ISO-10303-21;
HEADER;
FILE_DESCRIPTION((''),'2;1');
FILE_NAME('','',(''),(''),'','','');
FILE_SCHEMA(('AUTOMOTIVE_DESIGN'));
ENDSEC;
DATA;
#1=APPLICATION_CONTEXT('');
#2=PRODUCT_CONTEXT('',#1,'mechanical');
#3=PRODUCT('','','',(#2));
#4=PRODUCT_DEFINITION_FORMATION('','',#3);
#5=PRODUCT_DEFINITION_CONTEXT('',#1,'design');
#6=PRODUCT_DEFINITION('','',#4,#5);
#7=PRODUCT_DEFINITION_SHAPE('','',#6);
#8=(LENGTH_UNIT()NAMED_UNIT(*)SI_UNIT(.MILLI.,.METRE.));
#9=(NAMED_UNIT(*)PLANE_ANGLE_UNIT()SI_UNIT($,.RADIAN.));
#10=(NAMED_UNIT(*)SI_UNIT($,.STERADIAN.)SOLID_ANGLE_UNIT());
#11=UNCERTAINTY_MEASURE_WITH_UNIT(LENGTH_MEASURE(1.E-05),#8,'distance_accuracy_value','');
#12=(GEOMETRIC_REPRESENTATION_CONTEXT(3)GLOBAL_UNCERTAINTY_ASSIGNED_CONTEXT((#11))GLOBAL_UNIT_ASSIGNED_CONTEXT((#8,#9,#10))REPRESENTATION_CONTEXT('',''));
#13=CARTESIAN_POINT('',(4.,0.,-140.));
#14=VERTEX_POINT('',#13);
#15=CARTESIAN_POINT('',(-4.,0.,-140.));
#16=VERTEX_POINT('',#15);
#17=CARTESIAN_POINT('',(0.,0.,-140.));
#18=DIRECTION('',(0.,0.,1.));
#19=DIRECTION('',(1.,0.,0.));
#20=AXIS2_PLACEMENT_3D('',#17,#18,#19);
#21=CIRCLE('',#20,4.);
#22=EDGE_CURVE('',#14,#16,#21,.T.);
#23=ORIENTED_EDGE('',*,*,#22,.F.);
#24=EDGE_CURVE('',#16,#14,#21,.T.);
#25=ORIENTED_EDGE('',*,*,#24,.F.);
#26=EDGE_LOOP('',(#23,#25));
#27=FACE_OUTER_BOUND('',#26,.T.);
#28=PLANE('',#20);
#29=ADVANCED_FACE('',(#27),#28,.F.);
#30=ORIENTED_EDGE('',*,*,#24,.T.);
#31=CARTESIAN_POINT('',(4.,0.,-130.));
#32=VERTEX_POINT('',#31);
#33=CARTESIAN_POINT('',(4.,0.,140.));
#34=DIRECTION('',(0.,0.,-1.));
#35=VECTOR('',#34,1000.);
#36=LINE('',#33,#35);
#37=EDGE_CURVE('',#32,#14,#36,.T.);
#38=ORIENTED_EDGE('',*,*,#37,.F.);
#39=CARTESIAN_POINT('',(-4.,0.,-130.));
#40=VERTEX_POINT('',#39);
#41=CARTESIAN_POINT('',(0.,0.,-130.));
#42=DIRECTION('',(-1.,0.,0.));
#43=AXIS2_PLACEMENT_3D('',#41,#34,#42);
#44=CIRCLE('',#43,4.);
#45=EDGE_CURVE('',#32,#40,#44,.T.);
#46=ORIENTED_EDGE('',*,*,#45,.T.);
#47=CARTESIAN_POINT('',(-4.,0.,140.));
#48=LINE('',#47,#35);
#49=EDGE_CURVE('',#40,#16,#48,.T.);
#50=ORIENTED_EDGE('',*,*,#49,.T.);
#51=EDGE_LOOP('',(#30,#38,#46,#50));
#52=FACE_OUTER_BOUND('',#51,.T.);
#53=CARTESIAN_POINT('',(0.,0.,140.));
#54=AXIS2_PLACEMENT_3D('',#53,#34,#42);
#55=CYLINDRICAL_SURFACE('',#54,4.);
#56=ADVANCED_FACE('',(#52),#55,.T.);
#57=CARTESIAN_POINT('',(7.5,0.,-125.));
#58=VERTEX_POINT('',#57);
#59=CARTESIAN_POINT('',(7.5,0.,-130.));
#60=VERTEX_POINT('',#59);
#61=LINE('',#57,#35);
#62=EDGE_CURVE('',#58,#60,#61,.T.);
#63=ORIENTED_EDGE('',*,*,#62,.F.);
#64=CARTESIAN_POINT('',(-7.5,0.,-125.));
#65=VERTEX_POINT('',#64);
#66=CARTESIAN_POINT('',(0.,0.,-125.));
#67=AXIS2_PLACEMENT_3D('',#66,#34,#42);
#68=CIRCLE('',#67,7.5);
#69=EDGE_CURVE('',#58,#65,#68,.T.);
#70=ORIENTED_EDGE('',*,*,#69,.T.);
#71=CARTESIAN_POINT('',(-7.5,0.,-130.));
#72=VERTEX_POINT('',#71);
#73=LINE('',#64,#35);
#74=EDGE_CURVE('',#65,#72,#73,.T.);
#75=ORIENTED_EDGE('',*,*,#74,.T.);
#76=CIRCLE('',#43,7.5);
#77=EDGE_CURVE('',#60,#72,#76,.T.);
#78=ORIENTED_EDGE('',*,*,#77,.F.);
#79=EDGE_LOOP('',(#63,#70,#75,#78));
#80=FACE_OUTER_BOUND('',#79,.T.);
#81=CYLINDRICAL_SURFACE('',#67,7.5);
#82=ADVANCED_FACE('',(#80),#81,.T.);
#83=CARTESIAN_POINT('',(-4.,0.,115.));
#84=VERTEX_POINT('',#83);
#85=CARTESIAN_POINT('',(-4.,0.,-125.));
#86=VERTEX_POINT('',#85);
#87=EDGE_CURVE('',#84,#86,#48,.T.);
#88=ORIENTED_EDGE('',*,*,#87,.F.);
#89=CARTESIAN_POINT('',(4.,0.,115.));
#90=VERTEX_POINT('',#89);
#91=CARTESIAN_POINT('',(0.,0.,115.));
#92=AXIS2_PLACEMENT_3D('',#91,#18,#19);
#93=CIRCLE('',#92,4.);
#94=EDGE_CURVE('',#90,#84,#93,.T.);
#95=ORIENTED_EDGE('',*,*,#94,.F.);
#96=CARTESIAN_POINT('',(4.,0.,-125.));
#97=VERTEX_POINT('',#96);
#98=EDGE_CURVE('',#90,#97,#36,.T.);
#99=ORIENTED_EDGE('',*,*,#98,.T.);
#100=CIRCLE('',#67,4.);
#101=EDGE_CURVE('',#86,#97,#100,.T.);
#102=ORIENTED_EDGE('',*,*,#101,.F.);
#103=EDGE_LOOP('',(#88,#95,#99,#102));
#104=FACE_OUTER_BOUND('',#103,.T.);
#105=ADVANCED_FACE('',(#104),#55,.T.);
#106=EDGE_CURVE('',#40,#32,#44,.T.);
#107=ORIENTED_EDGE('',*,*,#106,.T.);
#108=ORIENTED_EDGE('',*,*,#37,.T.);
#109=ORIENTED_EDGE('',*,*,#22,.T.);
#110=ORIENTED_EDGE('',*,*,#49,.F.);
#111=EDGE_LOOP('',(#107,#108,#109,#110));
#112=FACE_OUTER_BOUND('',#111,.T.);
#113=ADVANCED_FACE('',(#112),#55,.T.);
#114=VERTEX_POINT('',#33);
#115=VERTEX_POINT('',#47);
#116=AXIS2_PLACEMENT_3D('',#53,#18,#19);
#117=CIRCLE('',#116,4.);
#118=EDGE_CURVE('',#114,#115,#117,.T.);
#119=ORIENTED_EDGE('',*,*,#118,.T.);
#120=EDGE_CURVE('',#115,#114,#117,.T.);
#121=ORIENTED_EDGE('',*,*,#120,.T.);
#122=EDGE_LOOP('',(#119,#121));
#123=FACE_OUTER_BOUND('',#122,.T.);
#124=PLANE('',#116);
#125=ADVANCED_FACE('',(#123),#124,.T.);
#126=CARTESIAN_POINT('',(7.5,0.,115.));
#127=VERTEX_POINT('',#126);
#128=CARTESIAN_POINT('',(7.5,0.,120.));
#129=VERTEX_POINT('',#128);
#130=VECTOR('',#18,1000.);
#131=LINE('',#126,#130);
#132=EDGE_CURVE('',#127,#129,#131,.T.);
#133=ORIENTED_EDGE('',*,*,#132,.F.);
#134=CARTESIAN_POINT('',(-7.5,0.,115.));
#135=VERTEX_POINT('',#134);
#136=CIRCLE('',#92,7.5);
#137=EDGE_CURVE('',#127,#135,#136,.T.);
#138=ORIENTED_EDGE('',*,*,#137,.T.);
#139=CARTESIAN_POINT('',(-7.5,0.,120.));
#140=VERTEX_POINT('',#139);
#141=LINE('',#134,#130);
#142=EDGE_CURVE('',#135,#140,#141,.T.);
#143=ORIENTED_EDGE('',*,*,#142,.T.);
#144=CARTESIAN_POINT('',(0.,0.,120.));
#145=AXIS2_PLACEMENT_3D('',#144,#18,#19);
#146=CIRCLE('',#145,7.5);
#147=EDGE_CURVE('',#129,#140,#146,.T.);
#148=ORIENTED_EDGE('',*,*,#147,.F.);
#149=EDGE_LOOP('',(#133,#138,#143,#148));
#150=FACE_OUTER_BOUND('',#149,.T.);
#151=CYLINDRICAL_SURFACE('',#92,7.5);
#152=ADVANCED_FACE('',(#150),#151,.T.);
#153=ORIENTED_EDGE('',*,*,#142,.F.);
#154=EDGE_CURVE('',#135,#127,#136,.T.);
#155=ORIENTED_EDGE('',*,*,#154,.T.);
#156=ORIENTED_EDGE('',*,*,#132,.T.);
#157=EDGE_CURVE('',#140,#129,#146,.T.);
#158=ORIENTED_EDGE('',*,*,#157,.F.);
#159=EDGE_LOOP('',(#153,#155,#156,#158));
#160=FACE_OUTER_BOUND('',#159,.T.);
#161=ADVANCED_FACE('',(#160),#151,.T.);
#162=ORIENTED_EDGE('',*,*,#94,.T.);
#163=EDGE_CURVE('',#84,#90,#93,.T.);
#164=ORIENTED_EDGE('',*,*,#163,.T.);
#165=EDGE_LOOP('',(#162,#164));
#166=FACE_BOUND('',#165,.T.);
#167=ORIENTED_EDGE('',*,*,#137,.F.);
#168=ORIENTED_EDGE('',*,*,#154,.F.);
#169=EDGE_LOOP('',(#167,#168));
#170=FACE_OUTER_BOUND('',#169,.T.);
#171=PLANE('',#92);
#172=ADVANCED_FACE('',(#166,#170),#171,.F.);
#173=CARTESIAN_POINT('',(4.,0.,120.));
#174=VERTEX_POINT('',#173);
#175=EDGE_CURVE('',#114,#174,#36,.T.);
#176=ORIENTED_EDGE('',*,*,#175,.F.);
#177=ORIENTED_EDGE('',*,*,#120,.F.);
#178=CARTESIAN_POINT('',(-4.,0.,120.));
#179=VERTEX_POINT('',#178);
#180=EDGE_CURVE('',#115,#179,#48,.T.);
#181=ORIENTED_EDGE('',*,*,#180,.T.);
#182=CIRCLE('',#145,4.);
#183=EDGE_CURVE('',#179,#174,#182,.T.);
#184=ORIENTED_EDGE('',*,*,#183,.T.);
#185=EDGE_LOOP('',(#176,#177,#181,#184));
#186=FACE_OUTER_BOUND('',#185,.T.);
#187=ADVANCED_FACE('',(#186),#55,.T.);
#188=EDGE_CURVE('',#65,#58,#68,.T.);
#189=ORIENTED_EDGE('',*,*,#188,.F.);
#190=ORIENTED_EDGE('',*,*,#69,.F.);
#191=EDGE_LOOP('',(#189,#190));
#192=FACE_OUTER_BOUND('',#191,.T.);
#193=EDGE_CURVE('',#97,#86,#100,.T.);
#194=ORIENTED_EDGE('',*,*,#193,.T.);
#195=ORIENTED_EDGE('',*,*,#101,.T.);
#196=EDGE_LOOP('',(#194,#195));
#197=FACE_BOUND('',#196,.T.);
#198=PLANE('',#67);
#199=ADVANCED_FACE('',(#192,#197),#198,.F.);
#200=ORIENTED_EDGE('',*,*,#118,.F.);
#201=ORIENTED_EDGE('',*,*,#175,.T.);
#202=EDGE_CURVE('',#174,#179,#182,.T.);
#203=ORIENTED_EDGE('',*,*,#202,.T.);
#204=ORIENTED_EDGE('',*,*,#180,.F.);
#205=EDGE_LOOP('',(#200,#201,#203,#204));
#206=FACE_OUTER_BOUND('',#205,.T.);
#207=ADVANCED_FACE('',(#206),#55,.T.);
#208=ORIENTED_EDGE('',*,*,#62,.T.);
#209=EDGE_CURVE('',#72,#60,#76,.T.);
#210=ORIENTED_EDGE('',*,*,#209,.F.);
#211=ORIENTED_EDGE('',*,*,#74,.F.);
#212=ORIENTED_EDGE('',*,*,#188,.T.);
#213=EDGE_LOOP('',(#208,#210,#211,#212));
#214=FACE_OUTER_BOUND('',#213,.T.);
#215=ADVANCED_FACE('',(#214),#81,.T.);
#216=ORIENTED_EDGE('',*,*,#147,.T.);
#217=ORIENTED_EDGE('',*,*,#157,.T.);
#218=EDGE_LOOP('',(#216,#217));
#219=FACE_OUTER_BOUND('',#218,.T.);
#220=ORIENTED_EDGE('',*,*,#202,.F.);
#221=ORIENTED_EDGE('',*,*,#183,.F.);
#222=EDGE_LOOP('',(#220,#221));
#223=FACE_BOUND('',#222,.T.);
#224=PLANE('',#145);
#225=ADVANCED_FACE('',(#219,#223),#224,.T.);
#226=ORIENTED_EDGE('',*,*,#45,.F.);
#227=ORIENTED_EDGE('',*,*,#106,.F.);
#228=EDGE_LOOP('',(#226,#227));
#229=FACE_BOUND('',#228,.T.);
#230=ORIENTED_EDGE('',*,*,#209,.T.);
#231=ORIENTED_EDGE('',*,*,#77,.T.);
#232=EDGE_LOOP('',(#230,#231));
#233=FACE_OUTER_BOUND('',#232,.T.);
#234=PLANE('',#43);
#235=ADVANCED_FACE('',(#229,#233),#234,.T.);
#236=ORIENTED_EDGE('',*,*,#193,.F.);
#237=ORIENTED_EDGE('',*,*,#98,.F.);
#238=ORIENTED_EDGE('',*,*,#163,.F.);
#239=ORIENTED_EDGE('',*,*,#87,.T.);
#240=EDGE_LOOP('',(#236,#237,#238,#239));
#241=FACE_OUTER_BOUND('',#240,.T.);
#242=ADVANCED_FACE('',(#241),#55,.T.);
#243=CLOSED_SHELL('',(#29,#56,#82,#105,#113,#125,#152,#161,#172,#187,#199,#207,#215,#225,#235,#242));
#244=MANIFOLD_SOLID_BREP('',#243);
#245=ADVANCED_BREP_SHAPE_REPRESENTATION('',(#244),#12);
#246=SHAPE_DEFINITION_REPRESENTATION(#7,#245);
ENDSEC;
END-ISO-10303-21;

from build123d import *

# Parameters (mm, degrees)
SKETCH_1_R      = 4
EXTRUDE_1_DEPTH = 140
EXTRUDE_START   = -20
SKETCH_2_R      = 7.5
EXTRUDE_2_DEPTH = 5
EXTRUDE_START_2 = -15
SKETCH_3_R      = 7.5
EXTRUDE_3_DEPTH = 5


with BuildPart() as part:
    # 草图1 → 凸台-拉伸1 (new, symmetric)
    with BuildSketch(Plane.XY):
        Circle(SKETCH_1_R)
    extrude(amount=EXTRUDE_1_DEPTH, both=True)

    # 草图2 → 凸台-拉伸2 (add)
    with BuildSketch(Plane.XY.offset(140).offset(EXTRUDE_START)):
        Circle(SKETCH_2_R)
    extrude(amount=-EXTRUDE_2_DEPTH)

    # 草图3 → 凸台-拉伸3 (add)
    with BuildSketch(Plane(origin=(0, 0, -140), x_dir=(-1, 0, 0), z_dir=(0, 0, -1)).offset(EXTRUDE_START_2)):
        with Locations(Location((0, 0, 0), (0, 0, 180))):
            Circle(SKETCH_3_R)
    extrude(amount=EXTRUDE_3_DEPTH)


solid = part.part
